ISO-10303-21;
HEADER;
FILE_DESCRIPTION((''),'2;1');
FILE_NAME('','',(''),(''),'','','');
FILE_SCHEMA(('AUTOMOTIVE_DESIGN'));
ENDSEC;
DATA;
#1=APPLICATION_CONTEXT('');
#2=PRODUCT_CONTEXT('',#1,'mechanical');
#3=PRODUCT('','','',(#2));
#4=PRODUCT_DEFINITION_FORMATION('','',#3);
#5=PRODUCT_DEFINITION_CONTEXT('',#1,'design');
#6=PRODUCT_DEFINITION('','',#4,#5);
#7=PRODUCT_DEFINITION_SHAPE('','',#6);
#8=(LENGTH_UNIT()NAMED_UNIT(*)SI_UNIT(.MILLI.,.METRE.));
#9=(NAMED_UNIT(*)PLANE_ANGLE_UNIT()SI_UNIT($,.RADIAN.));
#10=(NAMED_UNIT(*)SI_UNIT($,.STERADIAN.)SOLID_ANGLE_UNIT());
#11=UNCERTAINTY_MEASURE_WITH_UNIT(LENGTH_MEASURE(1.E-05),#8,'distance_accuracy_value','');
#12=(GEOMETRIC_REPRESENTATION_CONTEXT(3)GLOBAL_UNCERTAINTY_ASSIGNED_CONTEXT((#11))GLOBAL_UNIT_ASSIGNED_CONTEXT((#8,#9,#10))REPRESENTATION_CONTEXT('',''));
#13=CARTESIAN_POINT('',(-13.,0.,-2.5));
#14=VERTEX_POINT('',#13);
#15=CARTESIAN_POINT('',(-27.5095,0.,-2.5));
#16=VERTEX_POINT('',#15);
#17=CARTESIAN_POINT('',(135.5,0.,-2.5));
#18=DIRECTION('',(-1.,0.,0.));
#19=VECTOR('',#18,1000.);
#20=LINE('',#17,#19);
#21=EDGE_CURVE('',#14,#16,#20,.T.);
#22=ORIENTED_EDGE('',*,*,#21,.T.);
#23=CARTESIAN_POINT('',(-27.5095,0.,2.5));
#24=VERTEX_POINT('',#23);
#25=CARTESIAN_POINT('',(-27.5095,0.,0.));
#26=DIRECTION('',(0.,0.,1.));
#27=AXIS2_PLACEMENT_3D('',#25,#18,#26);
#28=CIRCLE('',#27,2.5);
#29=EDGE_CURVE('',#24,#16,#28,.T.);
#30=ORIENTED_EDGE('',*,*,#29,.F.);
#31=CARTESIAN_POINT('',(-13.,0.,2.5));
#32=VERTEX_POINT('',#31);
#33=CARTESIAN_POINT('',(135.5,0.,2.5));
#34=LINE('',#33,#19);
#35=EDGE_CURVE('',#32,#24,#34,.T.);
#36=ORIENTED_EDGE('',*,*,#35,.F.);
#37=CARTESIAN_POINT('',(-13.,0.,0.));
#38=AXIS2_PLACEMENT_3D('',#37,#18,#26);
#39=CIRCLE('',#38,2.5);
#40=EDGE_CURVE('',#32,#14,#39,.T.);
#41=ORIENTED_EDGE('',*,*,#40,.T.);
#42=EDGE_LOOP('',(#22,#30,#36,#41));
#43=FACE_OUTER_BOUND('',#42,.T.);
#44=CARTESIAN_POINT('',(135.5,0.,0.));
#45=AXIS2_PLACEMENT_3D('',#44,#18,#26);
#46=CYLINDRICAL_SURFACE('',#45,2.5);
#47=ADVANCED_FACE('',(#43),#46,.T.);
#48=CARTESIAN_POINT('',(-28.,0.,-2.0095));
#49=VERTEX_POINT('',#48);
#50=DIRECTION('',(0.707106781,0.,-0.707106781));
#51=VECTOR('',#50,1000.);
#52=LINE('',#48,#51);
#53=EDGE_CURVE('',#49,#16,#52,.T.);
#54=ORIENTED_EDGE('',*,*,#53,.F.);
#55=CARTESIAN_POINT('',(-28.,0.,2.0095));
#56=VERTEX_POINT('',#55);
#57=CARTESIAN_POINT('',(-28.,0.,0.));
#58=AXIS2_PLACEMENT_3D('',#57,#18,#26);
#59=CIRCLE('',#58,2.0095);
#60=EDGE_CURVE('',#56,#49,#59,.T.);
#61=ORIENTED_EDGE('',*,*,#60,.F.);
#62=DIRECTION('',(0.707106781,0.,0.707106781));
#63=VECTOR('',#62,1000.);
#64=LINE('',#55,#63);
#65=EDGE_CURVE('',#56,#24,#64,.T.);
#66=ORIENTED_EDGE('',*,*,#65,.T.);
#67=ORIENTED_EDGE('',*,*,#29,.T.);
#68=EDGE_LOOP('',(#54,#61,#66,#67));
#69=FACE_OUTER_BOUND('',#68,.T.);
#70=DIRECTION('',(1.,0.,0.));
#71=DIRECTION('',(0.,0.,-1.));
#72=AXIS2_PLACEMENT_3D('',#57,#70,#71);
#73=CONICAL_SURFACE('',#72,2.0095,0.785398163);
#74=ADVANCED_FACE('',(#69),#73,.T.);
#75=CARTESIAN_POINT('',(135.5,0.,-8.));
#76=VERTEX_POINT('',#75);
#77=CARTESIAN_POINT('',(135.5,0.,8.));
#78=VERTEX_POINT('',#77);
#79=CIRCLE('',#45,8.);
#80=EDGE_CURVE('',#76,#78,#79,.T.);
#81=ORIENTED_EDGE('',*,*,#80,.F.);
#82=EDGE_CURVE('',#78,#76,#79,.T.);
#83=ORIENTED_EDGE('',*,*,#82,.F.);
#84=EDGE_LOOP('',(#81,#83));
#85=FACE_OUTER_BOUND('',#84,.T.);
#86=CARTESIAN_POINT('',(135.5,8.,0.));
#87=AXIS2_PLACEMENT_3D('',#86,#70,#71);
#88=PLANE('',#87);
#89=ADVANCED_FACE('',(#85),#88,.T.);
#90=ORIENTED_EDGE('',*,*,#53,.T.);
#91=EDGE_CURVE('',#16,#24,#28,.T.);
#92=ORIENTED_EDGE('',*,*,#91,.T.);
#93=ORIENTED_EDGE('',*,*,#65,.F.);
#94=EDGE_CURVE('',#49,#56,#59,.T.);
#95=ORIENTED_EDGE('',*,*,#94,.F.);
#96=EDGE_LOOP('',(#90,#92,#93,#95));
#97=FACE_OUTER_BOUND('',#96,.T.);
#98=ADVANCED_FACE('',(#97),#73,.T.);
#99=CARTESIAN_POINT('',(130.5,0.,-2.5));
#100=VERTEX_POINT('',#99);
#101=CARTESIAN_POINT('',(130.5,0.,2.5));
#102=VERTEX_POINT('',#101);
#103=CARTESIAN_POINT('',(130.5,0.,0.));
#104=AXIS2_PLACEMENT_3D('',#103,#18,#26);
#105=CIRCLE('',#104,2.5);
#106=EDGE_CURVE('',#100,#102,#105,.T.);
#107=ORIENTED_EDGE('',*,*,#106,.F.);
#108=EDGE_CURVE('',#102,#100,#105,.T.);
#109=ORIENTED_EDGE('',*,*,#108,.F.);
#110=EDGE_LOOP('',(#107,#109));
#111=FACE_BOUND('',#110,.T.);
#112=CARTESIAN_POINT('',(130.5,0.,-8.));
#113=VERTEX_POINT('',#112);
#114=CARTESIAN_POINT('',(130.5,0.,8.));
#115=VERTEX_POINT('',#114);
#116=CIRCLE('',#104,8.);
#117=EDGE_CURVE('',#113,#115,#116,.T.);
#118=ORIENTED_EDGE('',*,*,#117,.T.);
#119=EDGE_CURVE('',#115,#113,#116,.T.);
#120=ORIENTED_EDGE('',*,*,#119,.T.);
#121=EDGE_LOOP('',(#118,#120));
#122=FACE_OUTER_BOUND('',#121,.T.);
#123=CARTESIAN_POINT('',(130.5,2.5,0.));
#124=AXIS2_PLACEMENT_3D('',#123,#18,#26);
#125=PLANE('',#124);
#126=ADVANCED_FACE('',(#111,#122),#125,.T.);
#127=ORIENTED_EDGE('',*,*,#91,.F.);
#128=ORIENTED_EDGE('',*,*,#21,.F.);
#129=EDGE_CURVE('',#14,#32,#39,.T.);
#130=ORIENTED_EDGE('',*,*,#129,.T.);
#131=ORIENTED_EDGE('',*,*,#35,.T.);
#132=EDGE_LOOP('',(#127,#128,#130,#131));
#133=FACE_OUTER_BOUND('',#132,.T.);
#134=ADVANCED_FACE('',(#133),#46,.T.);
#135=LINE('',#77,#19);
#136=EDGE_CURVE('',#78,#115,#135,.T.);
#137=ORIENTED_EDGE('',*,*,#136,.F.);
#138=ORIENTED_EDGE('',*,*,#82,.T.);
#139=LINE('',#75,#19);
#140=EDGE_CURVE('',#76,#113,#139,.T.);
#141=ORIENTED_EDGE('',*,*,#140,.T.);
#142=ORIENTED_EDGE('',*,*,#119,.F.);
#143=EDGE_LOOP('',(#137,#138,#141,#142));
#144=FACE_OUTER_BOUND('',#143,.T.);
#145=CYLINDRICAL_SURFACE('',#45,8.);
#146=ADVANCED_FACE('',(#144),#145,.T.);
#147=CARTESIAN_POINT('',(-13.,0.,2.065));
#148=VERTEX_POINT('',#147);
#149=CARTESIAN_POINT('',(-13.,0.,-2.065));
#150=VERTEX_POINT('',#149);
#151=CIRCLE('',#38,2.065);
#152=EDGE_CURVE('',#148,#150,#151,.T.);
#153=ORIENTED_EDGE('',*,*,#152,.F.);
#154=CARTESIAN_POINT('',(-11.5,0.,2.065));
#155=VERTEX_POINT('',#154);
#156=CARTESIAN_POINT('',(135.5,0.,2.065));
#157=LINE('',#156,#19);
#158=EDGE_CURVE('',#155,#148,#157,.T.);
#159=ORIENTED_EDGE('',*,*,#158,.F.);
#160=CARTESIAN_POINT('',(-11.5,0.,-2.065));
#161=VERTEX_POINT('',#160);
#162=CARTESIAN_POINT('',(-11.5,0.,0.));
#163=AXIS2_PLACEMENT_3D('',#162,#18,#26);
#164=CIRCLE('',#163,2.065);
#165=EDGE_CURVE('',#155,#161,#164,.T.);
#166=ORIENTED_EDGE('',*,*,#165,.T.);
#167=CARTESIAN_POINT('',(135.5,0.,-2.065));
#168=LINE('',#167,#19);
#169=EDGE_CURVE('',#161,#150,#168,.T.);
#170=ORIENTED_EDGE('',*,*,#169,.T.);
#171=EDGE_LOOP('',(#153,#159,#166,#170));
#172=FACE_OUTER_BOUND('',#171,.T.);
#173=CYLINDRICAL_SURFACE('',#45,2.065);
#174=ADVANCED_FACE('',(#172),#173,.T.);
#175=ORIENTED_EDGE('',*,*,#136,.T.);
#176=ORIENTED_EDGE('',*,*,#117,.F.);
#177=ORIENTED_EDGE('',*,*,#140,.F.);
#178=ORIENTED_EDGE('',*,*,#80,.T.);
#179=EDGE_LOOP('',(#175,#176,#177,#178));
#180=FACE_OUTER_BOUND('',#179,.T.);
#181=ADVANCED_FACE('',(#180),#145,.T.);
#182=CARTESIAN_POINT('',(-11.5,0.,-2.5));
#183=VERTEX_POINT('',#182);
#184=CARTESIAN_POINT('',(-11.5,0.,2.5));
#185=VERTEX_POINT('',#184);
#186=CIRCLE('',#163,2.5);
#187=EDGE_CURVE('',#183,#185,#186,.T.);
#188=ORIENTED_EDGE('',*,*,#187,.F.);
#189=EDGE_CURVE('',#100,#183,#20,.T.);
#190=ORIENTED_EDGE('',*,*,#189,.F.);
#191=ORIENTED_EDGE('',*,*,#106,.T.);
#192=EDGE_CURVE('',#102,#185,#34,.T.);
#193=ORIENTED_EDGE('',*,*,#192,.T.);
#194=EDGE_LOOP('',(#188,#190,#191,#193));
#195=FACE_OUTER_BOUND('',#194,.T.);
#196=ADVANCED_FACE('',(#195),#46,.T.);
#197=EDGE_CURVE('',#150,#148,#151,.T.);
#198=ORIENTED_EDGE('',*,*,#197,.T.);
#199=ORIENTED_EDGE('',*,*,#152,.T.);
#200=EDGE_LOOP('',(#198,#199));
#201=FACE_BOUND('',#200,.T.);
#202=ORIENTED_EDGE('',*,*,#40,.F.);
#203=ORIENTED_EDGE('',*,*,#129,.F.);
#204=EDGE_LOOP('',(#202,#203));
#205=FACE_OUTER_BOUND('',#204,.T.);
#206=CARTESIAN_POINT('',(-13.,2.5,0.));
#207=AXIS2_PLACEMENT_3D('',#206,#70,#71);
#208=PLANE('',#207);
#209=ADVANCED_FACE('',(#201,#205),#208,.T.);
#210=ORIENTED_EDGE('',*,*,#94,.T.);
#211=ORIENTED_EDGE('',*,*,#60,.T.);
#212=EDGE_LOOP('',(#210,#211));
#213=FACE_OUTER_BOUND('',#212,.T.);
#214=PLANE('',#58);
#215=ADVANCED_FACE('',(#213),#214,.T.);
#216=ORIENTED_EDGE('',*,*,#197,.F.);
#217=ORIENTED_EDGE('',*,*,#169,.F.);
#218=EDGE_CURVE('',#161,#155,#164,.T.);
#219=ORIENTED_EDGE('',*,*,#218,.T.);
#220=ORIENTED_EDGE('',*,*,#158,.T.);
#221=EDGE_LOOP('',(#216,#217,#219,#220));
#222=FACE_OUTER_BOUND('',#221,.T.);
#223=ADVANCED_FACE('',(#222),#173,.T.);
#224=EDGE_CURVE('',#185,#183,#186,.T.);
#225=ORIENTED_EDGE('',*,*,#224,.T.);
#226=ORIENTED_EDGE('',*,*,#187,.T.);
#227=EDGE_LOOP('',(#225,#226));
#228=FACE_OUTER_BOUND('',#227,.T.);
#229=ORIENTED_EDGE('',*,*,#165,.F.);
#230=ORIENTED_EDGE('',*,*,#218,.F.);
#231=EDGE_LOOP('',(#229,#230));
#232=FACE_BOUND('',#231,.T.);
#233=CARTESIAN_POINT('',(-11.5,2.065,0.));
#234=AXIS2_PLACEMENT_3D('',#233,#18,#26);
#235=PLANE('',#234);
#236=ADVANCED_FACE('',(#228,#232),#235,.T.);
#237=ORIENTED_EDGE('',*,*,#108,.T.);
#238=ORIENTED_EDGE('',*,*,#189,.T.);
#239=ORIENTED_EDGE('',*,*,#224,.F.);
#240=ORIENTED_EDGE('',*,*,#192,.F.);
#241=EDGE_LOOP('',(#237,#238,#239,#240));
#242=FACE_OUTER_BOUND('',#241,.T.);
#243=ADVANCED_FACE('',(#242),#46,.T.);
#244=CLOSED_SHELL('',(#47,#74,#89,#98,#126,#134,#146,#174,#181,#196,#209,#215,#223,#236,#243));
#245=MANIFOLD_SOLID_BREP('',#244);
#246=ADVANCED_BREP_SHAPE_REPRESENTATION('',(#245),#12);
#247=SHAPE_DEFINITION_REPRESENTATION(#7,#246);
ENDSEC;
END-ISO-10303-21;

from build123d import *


with BuildPart() as part:
    # Sketch1 → Revolve1 (revolve)
    with BuildSketch(Plane(origin=(0, 0, 0), x_dir=(-1, 0, 0), z_dir=(0, 0, -1)), mode=Mode.PRIVATE) as revolve1_sk:
        Polygon((-135.5, 8), (-135.5, 0), (28, 0), (28, 2.0095), (27.5095, 2.5), (13, 2.5), (13, 2.065), (11.5, 2.065), (11.5, 2.5), (-130.5, 2.5), (-130.5, 8), align=None)
    revolve(revolve1_sk.sketch.rotate(Axis((135.5, 0, 0), (-1, 0, 0)), 270), axis=Axis((135.5, 0, 0), (-1, 0, 0)))


solid = part.part
